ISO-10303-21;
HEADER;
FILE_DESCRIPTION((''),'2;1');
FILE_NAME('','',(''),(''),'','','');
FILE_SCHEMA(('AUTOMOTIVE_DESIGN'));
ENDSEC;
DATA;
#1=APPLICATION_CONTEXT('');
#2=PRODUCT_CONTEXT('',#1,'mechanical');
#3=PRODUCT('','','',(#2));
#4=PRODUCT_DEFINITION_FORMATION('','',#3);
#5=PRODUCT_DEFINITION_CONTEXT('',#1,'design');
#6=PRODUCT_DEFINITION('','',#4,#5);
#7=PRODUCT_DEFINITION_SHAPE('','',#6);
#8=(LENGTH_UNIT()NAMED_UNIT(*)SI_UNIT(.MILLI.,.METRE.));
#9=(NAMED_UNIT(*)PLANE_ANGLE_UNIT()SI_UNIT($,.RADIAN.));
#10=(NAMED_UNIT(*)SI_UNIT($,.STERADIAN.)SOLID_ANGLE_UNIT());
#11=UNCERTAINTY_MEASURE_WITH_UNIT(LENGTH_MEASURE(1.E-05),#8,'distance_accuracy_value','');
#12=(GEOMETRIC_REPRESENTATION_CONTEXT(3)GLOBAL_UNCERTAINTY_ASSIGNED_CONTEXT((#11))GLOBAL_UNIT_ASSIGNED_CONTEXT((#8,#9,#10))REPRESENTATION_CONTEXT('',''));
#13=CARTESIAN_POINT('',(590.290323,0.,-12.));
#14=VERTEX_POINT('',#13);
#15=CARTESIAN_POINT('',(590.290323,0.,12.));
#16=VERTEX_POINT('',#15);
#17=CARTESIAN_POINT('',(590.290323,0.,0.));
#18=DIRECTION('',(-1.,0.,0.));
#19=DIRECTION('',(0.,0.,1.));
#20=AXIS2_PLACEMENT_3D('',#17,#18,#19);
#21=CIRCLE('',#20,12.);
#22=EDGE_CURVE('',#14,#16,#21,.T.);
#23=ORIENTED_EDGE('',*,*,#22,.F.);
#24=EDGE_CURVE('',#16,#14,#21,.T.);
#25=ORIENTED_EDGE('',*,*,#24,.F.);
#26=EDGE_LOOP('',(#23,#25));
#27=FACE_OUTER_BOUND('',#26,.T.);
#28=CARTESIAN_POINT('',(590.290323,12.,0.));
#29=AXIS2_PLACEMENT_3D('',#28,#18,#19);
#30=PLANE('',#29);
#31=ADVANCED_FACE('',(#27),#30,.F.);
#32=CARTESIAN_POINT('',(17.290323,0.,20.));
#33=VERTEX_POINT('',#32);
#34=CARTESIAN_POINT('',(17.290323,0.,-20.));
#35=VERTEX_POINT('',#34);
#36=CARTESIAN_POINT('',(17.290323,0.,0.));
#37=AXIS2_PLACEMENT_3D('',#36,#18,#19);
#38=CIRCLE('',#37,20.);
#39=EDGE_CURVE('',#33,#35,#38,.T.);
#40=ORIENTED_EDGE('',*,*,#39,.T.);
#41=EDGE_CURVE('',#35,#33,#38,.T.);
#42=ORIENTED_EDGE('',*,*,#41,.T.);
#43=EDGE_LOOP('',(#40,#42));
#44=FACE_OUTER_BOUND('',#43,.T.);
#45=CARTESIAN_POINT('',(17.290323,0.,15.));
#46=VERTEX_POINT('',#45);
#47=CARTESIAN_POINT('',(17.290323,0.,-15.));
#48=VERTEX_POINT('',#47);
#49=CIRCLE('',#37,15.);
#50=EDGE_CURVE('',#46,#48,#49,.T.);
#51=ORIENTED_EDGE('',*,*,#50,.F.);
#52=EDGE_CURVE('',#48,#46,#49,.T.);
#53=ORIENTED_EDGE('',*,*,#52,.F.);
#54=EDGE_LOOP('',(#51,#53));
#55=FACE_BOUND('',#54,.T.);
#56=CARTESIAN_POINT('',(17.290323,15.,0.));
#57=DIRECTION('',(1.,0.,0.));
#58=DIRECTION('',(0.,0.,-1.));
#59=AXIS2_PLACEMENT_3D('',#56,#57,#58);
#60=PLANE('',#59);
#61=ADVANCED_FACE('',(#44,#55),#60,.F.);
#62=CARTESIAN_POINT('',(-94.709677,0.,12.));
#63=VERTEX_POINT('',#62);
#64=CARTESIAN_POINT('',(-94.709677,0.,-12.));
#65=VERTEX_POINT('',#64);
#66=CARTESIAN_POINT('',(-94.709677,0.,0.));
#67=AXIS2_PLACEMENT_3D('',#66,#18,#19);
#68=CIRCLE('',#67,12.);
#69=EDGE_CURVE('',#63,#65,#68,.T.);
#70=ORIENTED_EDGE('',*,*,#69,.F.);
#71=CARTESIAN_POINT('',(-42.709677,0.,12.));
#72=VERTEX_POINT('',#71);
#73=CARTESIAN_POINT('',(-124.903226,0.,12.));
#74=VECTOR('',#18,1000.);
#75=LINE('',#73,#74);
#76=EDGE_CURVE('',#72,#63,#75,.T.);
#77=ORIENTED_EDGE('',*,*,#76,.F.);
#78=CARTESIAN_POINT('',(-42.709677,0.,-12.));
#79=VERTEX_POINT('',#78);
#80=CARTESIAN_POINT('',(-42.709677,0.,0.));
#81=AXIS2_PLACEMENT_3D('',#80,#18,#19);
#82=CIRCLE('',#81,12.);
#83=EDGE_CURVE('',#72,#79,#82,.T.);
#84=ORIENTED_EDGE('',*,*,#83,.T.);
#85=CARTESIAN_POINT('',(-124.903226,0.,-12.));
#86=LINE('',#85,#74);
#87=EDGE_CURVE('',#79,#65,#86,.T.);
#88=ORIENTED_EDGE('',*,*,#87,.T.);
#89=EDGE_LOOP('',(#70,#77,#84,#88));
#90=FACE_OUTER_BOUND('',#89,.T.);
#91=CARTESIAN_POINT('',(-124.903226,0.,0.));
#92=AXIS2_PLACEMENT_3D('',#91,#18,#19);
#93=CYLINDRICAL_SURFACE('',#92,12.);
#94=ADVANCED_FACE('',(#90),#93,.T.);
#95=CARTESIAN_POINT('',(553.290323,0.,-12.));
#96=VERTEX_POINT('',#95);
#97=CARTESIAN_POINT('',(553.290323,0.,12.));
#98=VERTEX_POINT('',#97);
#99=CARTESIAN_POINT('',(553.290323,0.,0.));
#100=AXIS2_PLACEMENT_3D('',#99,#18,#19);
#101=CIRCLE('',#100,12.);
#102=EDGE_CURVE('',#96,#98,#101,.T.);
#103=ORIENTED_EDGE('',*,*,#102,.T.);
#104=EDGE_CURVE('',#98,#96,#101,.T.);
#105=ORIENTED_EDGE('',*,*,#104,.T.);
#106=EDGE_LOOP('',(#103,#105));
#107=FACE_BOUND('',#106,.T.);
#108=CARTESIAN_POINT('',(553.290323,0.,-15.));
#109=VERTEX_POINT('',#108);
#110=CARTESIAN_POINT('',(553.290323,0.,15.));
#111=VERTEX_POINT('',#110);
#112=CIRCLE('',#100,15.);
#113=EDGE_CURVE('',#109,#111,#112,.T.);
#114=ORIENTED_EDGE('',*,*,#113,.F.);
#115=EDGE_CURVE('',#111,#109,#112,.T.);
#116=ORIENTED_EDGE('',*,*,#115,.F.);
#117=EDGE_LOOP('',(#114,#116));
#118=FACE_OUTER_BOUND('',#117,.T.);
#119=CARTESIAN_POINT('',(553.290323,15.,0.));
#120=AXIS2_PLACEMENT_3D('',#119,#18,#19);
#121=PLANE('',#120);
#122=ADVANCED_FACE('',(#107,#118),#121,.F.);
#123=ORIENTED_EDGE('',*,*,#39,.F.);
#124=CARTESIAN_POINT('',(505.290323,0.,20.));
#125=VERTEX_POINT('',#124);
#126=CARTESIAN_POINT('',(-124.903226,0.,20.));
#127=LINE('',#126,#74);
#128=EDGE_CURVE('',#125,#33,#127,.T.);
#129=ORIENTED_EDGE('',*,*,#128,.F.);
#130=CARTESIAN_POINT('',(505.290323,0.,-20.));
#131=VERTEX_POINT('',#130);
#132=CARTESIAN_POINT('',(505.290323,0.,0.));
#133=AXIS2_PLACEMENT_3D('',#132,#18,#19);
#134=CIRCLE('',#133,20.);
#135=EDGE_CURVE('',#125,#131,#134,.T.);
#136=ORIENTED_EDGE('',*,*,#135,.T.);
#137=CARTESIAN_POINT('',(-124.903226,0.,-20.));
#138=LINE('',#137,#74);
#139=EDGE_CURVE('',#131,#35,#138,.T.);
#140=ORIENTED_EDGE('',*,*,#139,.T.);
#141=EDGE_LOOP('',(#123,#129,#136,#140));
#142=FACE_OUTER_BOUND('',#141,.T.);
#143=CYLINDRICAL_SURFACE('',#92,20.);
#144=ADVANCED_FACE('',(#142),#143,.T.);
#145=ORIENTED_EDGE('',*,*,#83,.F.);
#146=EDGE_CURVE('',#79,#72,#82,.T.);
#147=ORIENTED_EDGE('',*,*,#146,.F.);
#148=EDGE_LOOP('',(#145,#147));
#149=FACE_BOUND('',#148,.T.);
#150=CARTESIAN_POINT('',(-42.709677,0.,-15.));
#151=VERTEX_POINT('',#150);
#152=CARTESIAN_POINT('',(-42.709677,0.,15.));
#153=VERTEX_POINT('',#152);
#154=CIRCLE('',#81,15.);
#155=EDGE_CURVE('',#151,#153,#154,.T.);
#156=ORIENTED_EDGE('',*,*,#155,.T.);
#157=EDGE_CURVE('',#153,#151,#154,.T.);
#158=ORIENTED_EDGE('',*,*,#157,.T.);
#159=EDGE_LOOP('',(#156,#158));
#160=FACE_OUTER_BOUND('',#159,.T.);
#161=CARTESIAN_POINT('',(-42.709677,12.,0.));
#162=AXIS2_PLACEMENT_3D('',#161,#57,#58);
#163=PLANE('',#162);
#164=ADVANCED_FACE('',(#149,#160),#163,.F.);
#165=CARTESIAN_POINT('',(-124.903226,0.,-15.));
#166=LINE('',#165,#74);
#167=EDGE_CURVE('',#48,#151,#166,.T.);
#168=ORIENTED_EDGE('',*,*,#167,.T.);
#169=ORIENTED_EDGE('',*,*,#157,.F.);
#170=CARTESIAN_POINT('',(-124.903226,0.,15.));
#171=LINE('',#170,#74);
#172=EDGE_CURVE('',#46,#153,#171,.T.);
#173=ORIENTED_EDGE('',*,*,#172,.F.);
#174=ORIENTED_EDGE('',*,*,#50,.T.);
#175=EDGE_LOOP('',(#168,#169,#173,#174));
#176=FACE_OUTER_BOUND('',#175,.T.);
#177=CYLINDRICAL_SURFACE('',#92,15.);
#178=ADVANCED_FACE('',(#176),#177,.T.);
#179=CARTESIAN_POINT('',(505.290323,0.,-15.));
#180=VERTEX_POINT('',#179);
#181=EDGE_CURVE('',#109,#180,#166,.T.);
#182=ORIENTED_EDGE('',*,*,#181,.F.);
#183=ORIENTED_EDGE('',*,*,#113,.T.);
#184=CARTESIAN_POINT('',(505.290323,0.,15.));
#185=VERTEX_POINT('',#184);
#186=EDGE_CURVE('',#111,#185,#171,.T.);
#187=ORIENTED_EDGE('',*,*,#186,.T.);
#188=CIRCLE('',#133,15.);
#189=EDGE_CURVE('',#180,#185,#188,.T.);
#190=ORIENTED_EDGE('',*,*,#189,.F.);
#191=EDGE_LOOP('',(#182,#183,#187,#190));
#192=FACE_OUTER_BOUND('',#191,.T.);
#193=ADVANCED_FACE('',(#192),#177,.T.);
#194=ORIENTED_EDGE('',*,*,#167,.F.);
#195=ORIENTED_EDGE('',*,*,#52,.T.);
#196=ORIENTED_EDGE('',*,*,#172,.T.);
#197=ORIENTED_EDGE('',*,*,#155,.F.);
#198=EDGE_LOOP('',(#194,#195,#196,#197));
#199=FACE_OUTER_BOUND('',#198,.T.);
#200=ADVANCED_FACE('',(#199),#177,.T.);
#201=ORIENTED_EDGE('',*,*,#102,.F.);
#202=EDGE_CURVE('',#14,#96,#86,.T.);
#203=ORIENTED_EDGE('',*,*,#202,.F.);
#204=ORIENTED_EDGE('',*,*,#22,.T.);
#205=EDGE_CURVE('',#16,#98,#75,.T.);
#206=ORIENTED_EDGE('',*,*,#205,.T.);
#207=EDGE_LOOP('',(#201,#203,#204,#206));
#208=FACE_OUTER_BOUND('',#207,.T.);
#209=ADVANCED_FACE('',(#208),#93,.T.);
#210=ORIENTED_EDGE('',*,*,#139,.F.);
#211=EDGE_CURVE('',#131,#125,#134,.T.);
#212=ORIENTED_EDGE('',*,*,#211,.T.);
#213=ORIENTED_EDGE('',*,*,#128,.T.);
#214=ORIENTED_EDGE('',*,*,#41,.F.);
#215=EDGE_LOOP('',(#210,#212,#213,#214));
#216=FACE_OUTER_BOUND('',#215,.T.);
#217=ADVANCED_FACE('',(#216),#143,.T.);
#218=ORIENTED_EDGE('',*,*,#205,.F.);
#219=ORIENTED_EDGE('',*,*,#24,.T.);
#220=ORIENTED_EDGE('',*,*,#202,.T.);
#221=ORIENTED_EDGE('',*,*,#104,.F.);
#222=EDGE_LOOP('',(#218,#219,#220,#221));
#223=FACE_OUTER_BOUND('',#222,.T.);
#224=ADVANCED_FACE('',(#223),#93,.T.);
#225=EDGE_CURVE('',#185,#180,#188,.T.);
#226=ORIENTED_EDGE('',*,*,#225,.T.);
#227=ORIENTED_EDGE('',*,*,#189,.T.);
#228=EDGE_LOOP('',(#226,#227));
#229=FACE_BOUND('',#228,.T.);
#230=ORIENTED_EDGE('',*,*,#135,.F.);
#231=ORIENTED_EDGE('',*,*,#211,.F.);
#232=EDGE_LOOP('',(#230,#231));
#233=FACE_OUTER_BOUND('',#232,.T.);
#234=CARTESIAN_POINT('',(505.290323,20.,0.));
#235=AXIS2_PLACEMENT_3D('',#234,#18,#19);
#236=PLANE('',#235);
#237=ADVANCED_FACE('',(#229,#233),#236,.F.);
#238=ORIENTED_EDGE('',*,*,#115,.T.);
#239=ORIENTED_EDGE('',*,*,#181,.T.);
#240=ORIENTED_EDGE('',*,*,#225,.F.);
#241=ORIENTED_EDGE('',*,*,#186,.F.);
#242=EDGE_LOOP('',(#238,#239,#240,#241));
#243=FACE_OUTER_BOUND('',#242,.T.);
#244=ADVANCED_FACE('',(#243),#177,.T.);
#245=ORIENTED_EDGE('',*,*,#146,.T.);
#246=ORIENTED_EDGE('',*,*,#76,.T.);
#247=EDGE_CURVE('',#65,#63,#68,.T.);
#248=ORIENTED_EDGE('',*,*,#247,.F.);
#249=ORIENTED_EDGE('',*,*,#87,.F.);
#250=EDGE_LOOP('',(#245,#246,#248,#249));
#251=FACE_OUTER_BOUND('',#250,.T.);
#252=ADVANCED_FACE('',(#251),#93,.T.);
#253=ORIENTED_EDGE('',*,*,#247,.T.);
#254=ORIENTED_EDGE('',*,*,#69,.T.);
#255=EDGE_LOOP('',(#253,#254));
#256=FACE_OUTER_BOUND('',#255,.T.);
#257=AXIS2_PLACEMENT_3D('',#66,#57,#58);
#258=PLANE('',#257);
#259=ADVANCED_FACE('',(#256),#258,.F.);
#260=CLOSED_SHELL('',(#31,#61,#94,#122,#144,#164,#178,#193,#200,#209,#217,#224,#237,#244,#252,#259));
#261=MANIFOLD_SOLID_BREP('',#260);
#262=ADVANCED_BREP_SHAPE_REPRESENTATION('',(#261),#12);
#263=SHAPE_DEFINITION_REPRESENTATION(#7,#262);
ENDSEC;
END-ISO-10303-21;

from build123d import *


with BuildPart() as part:
    # 草图1 → 旋转1 (revolve)
    with BuildSketch(Plane.XY, mode=Mode.PRIVATE) as revolve_1_sk:
        Polygon((-94.709677419, 0), (-94.709677419, 12), (-42.709677419, 12), (-42.709677419, 15), (17.290322581, 15), (17.290322581, 20), (505.290322581, 20), (505.290322581, 15), (553.290322581, 15), (553.290322581, 12), (590.290322581, 12), (590.290322581, 0), align=None)
    revolve(revolve_1_sk.sketch.rotate(Axis((-124.903225806, 0, 0), (1, 0, 0)), 90), axis=Axis((-124.903225806, 0, 0), (1, 0, 0)))


solid = part.part
